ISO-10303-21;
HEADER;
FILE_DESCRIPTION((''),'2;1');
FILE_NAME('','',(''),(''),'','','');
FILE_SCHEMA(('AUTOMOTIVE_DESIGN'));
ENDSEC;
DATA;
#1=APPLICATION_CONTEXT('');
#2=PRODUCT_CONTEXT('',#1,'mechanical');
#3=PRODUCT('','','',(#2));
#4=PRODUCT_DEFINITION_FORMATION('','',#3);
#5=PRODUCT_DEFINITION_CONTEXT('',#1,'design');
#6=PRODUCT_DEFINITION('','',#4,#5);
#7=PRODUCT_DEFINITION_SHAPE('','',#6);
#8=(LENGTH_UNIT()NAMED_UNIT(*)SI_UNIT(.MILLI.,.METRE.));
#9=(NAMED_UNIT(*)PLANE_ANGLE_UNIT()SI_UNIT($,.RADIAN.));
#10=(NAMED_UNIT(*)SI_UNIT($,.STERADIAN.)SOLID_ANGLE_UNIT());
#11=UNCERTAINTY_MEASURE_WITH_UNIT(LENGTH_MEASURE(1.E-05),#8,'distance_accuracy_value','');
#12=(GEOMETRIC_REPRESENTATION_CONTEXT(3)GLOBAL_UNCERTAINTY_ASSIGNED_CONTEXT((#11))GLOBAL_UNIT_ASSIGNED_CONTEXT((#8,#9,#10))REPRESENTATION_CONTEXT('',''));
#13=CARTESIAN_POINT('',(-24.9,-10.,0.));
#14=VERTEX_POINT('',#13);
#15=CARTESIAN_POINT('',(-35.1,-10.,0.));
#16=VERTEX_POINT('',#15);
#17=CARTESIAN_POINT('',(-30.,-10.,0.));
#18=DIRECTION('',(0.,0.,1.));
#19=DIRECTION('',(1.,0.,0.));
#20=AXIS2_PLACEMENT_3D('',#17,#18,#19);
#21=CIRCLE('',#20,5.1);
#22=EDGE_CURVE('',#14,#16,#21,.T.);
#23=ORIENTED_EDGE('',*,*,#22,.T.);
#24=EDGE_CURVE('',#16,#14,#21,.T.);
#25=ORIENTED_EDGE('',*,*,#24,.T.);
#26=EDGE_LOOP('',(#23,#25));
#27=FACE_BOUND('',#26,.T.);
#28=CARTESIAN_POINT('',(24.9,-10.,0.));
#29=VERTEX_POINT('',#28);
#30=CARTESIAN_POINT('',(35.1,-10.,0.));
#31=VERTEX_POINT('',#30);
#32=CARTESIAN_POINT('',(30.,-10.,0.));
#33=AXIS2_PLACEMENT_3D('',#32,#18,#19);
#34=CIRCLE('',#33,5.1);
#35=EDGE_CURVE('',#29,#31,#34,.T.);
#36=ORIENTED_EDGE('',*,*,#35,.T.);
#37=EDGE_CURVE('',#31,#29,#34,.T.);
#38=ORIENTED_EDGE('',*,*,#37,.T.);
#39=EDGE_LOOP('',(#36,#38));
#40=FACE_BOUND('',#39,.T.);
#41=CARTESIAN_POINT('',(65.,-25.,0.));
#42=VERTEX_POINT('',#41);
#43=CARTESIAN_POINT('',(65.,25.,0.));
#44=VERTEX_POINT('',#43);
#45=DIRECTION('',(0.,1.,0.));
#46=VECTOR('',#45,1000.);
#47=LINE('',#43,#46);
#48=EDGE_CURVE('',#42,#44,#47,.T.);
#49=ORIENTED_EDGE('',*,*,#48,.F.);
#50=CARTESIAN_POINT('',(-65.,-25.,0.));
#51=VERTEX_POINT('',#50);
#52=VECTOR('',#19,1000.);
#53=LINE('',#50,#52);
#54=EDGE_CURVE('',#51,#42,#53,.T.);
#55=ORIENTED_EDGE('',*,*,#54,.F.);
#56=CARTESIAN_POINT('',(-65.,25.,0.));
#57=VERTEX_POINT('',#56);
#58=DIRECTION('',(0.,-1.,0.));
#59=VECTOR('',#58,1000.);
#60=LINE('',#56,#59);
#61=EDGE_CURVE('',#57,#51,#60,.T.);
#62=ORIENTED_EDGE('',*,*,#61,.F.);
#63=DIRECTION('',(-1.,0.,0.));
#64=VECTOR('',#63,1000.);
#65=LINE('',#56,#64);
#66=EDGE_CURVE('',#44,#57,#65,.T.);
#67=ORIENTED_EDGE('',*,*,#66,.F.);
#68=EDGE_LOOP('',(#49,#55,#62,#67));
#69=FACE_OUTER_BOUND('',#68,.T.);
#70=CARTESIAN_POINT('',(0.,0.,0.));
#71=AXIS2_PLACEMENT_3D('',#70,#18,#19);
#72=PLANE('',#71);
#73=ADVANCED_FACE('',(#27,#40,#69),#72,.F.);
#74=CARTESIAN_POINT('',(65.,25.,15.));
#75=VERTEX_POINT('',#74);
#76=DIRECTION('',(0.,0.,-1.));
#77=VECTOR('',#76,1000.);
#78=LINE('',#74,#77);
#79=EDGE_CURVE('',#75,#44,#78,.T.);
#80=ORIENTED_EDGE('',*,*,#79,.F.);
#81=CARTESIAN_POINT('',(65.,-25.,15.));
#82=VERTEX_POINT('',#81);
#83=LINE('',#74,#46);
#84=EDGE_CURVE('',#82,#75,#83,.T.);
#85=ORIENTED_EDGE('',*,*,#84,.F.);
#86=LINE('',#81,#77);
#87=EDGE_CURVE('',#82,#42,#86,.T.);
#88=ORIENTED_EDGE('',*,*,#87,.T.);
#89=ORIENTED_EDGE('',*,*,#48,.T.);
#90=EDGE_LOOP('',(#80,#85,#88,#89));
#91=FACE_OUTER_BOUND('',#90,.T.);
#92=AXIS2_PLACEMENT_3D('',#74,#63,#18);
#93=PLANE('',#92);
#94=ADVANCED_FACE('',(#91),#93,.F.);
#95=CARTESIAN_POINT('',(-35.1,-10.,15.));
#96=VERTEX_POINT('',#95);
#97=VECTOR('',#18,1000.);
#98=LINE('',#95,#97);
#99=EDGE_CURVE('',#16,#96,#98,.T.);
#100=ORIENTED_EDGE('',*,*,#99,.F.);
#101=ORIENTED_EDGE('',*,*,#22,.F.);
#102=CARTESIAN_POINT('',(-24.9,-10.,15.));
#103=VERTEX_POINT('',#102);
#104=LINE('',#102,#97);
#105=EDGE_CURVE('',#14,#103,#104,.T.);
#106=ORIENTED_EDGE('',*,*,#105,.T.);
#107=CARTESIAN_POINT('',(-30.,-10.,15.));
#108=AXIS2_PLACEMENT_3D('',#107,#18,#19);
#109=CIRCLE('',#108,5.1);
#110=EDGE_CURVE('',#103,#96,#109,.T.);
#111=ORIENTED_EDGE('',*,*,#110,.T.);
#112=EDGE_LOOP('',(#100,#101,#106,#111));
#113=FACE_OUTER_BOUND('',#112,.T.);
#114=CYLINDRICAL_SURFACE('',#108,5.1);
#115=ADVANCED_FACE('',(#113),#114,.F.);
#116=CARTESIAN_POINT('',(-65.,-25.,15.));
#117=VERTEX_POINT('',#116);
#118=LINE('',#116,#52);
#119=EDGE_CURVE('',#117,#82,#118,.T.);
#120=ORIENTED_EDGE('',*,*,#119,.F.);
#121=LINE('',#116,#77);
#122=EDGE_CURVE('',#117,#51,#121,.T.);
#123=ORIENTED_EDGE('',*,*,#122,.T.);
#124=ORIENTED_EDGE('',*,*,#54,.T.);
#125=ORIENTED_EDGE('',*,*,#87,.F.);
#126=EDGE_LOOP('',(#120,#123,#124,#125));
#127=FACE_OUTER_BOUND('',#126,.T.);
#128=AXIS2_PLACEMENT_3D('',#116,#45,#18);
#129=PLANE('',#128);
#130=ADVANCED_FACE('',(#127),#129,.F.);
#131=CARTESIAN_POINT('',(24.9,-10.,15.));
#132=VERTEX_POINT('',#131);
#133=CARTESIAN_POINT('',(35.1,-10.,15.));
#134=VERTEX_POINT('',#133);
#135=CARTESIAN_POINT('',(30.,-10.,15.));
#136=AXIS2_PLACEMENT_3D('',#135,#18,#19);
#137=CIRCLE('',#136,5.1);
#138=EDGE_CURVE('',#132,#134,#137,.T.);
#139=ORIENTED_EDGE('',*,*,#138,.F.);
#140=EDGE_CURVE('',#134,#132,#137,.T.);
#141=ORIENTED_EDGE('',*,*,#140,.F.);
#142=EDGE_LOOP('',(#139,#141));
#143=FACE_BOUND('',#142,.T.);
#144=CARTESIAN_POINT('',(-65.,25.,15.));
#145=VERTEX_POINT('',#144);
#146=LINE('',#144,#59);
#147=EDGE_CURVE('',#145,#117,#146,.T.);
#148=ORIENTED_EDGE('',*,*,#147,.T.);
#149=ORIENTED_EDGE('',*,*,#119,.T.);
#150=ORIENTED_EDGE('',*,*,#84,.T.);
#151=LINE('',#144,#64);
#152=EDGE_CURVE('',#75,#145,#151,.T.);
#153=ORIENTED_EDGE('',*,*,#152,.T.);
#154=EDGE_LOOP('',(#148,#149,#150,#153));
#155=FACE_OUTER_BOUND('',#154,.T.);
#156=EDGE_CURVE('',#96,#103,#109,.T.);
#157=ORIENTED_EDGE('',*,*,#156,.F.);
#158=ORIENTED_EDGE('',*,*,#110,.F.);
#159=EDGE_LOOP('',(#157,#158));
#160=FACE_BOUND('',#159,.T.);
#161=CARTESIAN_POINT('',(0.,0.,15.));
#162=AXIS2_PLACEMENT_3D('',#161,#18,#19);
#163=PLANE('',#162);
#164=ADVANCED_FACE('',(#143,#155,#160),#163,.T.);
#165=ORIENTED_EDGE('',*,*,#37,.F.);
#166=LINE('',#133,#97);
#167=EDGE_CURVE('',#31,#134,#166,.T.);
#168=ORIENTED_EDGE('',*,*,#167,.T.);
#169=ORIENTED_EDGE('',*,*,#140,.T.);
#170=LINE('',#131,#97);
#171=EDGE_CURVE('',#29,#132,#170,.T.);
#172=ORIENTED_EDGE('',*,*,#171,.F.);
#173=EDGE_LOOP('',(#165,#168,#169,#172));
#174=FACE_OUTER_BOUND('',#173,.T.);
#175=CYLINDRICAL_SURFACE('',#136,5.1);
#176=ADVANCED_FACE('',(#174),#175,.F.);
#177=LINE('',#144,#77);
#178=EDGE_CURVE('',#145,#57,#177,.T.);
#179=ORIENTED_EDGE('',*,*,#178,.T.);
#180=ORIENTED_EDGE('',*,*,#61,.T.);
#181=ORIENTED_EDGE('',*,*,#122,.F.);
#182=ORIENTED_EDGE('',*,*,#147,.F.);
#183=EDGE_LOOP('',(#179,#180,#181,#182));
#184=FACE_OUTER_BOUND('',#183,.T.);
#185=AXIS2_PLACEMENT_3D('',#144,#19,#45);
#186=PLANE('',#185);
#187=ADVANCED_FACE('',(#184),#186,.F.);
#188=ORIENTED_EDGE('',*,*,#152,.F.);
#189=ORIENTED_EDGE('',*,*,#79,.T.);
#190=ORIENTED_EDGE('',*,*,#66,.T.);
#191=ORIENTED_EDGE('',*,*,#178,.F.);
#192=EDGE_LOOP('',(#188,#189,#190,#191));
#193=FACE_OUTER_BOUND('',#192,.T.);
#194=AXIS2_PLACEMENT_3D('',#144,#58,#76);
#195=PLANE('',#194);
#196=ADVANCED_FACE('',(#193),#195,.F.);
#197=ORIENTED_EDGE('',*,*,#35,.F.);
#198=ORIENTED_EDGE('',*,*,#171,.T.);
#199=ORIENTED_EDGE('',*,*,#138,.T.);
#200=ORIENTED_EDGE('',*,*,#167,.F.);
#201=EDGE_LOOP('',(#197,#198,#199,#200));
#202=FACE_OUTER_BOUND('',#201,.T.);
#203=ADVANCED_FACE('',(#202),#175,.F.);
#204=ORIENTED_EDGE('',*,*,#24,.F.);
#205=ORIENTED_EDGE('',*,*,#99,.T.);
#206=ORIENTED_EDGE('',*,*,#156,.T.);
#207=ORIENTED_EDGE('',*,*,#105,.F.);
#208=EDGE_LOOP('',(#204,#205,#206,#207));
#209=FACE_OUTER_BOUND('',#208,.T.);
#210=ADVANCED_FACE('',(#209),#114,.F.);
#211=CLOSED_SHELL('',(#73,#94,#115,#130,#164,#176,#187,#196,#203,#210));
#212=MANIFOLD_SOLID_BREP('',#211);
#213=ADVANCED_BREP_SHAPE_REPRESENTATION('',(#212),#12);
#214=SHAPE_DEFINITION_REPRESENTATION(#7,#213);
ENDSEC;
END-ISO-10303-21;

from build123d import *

# Parameters (mm, degrees)
SKETCH1_W              = 130
SKETCH1_H              = 50
BOSS_EXTRUDE1_DEPTH    = 15
M12_TAPPED_HOLE1_D     = 10.2
M12_TAPPED_HOLE1_DEPTH = 29.25
M12_TAPPED_HOLE1_TIP   = 3.064389157


with BuildPart() as part:
    # Sketch1 → Boss-Extrude1 (new body)
    with BuildSketch(Plane.XY):
        Rectangle(SKETCH1_W, SKETCH1_H)
    extrude(amount=BOSS_EXTRUDE1_DEPTH)

    # M12 Tapped Hole1
    with Locations(Plane.XY.offset(15)):
        with Locations((-30, -10), (30, -10)):
            Hole(M12_TAPPED_HOLE1_D / 2, depth=M12_TAPPED_HOLE1_DEPTH)
            with Locations((0, 0, -(M12_TAPPED_HOLE1_DEPTH + M12_TAPPED_HOLE1_TIP / 2))):  # 118° drill point
                Cone(0, M12_TAPPED_HOLE1_D / 2, M12_TAPPED_HOLE1_TIP, mode=Mode.SUBTRACT)


solid = part.part
